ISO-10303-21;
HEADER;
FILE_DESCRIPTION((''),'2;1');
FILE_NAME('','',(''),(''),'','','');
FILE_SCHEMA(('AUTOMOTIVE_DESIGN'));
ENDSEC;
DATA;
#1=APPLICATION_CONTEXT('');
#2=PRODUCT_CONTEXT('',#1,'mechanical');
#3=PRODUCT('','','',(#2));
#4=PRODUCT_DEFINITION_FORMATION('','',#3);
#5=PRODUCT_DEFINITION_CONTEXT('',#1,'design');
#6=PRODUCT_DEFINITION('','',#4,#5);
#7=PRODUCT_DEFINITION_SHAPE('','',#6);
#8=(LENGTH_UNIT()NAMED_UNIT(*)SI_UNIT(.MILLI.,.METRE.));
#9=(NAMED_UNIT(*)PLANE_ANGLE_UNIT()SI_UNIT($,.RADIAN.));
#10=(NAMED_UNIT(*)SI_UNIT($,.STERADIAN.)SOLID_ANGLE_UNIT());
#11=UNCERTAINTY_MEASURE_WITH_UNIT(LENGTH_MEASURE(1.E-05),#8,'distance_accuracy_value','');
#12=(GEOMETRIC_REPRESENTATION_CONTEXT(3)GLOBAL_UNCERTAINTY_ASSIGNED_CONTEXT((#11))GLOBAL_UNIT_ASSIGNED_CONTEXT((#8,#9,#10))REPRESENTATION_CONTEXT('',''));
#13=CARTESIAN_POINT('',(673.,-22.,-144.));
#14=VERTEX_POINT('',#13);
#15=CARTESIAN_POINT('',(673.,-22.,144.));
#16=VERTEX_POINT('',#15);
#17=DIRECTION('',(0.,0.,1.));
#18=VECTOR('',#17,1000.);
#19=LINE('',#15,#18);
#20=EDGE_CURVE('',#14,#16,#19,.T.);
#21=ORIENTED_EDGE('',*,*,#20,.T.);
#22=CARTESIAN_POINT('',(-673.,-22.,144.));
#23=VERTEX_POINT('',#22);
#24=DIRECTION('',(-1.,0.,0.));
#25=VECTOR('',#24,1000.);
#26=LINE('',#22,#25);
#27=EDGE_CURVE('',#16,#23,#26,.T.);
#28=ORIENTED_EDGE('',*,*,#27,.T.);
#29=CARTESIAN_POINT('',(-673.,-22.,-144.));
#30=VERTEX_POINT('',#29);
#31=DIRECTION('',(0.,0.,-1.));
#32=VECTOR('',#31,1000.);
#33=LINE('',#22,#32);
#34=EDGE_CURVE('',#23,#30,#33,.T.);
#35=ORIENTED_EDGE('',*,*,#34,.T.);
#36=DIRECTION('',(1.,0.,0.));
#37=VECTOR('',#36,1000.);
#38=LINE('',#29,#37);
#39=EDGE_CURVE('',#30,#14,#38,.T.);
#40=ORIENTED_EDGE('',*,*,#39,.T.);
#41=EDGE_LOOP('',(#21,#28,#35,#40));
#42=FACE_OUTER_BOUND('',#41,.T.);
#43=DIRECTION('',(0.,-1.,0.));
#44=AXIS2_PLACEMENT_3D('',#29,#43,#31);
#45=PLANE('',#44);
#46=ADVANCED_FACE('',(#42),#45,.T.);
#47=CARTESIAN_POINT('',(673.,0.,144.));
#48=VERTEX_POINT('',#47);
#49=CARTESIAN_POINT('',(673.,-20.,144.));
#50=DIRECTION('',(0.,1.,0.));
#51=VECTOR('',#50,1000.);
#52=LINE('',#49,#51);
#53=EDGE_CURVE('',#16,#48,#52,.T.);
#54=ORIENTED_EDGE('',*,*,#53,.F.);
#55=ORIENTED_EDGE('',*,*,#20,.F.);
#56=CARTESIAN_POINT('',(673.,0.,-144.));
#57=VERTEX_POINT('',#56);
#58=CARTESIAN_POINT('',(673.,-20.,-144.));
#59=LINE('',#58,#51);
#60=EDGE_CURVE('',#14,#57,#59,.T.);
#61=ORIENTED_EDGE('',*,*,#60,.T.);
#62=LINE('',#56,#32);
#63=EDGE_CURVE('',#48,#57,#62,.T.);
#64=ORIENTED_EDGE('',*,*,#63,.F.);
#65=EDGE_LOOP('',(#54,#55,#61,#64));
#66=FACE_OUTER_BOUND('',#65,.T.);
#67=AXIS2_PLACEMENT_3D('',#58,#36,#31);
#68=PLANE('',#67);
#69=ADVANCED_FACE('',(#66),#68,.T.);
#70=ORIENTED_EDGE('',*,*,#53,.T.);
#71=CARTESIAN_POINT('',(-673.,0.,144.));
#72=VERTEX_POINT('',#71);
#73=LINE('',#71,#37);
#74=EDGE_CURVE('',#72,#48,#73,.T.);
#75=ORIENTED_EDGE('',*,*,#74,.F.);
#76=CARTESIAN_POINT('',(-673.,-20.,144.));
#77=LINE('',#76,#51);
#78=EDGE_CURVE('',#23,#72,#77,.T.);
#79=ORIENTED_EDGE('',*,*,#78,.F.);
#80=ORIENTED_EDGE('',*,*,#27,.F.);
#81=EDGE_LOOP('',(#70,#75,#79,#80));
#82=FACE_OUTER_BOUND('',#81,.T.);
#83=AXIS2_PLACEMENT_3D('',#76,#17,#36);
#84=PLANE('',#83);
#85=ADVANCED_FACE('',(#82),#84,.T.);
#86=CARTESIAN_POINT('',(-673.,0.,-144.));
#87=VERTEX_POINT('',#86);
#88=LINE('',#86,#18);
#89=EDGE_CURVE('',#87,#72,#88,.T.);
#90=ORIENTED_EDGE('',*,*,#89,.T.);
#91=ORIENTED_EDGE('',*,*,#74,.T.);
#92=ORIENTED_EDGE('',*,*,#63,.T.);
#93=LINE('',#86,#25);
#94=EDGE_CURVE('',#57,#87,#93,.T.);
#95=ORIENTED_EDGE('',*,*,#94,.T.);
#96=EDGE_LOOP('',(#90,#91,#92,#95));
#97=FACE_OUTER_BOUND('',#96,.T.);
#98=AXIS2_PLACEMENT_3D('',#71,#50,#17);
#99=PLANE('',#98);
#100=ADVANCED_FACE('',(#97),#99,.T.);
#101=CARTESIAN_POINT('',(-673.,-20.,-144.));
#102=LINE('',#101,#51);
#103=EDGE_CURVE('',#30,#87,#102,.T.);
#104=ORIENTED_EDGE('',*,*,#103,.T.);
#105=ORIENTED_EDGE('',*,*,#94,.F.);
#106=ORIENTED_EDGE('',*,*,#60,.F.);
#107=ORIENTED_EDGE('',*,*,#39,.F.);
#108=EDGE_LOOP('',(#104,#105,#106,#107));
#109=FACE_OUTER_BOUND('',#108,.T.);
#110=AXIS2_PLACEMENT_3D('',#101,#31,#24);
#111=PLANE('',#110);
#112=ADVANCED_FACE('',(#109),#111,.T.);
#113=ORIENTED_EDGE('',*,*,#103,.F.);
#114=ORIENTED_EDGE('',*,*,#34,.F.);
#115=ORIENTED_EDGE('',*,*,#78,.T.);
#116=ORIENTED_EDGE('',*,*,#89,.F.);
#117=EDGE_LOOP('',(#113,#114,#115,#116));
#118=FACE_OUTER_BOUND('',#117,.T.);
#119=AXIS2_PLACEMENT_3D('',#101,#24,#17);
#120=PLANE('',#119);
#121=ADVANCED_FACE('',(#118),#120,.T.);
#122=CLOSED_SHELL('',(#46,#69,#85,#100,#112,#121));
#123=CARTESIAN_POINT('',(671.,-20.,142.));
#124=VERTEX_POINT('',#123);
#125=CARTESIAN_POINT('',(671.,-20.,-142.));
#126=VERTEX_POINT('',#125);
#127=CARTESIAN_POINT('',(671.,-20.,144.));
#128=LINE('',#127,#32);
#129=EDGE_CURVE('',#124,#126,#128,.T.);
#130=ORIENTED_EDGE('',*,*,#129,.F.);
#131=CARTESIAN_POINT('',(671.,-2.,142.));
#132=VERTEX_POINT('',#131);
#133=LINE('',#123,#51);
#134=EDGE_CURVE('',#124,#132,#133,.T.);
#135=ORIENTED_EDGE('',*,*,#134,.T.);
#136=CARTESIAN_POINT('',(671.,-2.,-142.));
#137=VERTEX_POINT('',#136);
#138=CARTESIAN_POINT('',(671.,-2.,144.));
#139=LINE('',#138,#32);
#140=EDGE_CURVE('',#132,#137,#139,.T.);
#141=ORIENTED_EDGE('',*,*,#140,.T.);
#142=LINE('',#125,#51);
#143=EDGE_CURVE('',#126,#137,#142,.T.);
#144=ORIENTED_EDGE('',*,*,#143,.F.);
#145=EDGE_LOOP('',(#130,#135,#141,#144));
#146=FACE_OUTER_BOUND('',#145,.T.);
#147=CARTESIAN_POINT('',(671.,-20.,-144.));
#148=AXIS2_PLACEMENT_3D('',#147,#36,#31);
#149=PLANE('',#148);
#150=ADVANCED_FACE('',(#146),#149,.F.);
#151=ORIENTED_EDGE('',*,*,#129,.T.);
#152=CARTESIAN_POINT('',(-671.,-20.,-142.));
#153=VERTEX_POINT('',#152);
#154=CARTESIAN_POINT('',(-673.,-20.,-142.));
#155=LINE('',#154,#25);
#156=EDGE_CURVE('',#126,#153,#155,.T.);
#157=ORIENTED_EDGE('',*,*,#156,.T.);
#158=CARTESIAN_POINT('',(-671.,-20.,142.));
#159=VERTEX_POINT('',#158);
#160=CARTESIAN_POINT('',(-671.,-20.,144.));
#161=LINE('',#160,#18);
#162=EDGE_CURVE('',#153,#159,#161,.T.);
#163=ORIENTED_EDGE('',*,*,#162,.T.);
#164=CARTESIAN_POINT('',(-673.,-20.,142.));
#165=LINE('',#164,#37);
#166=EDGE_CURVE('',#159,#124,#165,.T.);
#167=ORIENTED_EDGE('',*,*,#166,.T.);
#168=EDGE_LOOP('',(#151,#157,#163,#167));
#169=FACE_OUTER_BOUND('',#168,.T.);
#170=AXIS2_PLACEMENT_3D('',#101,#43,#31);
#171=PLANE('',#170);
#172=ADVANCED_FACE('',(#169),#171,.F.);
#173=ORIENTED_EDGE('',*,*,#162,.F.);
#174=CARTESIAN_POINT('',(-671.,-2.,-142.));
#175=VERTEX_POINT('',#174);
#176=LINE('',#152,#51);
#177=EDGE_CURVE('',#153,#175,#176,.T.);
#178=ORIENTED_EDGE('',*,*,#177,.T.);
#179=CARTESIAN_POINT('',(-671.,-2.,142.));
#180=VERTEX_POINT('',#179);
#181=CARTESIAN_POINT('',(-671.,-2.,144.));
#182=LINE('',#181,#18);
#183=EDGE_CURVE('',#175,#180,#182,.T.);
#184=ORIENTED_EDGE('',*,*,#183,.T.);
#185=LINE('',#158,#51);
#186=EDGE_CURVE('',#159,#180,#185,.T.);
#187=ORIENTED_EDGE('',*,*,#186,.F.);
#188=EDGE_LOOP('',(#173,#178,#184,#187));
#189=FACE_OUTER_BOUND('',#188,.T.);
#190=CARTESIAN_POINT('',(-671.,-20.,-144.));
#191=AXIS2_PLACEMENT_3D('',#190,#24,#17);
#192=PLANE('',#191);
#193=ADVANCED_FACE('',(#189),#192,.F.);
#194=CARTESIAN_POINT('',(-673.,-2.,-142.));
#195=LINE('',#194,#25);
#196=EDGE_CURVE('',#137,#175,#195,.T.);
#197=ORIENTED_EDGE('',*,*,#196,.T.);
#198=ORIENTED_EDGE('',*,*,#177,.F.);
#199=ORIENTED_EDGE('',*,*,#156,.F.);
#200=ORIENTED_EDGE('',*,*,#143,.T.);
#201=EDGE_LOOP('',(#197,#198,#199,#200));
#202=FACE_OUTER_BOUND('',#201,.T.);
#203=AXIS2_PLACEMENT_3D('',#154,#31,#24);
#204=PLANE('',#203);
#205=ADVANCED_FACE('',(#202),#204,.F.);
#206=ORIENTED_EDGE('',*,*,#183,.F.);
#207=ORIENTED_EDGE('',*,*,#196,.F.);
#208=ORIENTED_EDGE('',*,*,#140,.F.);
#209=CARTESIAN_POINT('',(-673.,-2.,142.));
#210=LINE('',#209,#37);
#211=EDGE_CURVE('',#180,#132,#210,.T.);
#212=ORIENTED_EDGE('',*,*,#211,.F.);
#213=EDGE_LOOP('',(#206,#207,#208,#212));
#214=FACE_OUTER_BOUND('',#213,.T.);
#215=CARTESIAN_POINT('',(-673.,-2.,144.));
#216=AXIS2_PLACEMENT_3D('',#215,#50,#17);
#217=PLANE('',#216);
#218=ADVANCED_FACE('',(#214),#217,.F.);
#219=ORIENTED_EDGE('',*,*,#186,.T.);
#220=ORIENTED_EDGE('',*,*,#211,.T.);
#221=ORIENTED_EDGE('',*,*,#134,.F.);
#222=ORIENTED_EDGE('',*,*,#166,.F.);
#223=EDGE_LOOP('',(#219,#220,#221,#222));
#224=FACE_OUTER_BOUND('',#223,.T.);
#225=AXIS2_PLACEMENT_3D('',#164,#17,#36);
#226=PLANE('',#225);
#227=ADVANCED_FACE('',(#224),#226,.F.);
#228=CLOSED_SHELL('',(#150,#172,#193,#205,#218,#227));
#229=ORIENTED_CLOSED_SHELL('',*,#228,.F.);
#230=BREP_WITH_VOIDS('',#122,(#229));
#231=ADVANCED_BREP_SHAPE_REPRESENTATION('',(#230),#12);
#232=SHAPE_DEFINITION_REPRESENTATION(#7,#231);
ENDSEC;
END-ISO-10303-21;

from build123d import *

# Parameters (mm, degrees)
SKETCH_1_W      = 1346
SKETCH_1_H      = 288
EXTRUDE_1_DEPTH = 20
SHELL_1_T       = -2
SKETCH_2_W      = 1346
SKETCH_2_H      = 288
EXTRUDE_2_DEPTH = 2


with BuildPart() as part:
    # 草图1 → 凸台-拉伸1 (new body)
    with BuildSketch(Plane(origin=(0, 0, 0), x_dir=(1, 0, 0), z_dir=(0, 1, 0))):
        Rectangle(SKETCH_1_W, SKETCH_1_H)
    extrude(amount=-EXTRUDE_1_DEPTH)

    # 抽壳1
    shell_1_openings = [part.faces().sort_by_distance(p)[0] for p in [
        (0, -20, 0),
    ]]
    offset(amount=SHELL_1_T, openings=shell_1_openings, kind=Kind.INTERSECTION)

    # 草图2 → 凸台-拉伸2 (add)
    with BuildSketch(Plane.XZ.offset(20)):
        Rectangle(SKETCH_2_W, SKETCH_2_H)
    extrude(amount=EXTRUDE_2_DEPTH)


solid = part.part
